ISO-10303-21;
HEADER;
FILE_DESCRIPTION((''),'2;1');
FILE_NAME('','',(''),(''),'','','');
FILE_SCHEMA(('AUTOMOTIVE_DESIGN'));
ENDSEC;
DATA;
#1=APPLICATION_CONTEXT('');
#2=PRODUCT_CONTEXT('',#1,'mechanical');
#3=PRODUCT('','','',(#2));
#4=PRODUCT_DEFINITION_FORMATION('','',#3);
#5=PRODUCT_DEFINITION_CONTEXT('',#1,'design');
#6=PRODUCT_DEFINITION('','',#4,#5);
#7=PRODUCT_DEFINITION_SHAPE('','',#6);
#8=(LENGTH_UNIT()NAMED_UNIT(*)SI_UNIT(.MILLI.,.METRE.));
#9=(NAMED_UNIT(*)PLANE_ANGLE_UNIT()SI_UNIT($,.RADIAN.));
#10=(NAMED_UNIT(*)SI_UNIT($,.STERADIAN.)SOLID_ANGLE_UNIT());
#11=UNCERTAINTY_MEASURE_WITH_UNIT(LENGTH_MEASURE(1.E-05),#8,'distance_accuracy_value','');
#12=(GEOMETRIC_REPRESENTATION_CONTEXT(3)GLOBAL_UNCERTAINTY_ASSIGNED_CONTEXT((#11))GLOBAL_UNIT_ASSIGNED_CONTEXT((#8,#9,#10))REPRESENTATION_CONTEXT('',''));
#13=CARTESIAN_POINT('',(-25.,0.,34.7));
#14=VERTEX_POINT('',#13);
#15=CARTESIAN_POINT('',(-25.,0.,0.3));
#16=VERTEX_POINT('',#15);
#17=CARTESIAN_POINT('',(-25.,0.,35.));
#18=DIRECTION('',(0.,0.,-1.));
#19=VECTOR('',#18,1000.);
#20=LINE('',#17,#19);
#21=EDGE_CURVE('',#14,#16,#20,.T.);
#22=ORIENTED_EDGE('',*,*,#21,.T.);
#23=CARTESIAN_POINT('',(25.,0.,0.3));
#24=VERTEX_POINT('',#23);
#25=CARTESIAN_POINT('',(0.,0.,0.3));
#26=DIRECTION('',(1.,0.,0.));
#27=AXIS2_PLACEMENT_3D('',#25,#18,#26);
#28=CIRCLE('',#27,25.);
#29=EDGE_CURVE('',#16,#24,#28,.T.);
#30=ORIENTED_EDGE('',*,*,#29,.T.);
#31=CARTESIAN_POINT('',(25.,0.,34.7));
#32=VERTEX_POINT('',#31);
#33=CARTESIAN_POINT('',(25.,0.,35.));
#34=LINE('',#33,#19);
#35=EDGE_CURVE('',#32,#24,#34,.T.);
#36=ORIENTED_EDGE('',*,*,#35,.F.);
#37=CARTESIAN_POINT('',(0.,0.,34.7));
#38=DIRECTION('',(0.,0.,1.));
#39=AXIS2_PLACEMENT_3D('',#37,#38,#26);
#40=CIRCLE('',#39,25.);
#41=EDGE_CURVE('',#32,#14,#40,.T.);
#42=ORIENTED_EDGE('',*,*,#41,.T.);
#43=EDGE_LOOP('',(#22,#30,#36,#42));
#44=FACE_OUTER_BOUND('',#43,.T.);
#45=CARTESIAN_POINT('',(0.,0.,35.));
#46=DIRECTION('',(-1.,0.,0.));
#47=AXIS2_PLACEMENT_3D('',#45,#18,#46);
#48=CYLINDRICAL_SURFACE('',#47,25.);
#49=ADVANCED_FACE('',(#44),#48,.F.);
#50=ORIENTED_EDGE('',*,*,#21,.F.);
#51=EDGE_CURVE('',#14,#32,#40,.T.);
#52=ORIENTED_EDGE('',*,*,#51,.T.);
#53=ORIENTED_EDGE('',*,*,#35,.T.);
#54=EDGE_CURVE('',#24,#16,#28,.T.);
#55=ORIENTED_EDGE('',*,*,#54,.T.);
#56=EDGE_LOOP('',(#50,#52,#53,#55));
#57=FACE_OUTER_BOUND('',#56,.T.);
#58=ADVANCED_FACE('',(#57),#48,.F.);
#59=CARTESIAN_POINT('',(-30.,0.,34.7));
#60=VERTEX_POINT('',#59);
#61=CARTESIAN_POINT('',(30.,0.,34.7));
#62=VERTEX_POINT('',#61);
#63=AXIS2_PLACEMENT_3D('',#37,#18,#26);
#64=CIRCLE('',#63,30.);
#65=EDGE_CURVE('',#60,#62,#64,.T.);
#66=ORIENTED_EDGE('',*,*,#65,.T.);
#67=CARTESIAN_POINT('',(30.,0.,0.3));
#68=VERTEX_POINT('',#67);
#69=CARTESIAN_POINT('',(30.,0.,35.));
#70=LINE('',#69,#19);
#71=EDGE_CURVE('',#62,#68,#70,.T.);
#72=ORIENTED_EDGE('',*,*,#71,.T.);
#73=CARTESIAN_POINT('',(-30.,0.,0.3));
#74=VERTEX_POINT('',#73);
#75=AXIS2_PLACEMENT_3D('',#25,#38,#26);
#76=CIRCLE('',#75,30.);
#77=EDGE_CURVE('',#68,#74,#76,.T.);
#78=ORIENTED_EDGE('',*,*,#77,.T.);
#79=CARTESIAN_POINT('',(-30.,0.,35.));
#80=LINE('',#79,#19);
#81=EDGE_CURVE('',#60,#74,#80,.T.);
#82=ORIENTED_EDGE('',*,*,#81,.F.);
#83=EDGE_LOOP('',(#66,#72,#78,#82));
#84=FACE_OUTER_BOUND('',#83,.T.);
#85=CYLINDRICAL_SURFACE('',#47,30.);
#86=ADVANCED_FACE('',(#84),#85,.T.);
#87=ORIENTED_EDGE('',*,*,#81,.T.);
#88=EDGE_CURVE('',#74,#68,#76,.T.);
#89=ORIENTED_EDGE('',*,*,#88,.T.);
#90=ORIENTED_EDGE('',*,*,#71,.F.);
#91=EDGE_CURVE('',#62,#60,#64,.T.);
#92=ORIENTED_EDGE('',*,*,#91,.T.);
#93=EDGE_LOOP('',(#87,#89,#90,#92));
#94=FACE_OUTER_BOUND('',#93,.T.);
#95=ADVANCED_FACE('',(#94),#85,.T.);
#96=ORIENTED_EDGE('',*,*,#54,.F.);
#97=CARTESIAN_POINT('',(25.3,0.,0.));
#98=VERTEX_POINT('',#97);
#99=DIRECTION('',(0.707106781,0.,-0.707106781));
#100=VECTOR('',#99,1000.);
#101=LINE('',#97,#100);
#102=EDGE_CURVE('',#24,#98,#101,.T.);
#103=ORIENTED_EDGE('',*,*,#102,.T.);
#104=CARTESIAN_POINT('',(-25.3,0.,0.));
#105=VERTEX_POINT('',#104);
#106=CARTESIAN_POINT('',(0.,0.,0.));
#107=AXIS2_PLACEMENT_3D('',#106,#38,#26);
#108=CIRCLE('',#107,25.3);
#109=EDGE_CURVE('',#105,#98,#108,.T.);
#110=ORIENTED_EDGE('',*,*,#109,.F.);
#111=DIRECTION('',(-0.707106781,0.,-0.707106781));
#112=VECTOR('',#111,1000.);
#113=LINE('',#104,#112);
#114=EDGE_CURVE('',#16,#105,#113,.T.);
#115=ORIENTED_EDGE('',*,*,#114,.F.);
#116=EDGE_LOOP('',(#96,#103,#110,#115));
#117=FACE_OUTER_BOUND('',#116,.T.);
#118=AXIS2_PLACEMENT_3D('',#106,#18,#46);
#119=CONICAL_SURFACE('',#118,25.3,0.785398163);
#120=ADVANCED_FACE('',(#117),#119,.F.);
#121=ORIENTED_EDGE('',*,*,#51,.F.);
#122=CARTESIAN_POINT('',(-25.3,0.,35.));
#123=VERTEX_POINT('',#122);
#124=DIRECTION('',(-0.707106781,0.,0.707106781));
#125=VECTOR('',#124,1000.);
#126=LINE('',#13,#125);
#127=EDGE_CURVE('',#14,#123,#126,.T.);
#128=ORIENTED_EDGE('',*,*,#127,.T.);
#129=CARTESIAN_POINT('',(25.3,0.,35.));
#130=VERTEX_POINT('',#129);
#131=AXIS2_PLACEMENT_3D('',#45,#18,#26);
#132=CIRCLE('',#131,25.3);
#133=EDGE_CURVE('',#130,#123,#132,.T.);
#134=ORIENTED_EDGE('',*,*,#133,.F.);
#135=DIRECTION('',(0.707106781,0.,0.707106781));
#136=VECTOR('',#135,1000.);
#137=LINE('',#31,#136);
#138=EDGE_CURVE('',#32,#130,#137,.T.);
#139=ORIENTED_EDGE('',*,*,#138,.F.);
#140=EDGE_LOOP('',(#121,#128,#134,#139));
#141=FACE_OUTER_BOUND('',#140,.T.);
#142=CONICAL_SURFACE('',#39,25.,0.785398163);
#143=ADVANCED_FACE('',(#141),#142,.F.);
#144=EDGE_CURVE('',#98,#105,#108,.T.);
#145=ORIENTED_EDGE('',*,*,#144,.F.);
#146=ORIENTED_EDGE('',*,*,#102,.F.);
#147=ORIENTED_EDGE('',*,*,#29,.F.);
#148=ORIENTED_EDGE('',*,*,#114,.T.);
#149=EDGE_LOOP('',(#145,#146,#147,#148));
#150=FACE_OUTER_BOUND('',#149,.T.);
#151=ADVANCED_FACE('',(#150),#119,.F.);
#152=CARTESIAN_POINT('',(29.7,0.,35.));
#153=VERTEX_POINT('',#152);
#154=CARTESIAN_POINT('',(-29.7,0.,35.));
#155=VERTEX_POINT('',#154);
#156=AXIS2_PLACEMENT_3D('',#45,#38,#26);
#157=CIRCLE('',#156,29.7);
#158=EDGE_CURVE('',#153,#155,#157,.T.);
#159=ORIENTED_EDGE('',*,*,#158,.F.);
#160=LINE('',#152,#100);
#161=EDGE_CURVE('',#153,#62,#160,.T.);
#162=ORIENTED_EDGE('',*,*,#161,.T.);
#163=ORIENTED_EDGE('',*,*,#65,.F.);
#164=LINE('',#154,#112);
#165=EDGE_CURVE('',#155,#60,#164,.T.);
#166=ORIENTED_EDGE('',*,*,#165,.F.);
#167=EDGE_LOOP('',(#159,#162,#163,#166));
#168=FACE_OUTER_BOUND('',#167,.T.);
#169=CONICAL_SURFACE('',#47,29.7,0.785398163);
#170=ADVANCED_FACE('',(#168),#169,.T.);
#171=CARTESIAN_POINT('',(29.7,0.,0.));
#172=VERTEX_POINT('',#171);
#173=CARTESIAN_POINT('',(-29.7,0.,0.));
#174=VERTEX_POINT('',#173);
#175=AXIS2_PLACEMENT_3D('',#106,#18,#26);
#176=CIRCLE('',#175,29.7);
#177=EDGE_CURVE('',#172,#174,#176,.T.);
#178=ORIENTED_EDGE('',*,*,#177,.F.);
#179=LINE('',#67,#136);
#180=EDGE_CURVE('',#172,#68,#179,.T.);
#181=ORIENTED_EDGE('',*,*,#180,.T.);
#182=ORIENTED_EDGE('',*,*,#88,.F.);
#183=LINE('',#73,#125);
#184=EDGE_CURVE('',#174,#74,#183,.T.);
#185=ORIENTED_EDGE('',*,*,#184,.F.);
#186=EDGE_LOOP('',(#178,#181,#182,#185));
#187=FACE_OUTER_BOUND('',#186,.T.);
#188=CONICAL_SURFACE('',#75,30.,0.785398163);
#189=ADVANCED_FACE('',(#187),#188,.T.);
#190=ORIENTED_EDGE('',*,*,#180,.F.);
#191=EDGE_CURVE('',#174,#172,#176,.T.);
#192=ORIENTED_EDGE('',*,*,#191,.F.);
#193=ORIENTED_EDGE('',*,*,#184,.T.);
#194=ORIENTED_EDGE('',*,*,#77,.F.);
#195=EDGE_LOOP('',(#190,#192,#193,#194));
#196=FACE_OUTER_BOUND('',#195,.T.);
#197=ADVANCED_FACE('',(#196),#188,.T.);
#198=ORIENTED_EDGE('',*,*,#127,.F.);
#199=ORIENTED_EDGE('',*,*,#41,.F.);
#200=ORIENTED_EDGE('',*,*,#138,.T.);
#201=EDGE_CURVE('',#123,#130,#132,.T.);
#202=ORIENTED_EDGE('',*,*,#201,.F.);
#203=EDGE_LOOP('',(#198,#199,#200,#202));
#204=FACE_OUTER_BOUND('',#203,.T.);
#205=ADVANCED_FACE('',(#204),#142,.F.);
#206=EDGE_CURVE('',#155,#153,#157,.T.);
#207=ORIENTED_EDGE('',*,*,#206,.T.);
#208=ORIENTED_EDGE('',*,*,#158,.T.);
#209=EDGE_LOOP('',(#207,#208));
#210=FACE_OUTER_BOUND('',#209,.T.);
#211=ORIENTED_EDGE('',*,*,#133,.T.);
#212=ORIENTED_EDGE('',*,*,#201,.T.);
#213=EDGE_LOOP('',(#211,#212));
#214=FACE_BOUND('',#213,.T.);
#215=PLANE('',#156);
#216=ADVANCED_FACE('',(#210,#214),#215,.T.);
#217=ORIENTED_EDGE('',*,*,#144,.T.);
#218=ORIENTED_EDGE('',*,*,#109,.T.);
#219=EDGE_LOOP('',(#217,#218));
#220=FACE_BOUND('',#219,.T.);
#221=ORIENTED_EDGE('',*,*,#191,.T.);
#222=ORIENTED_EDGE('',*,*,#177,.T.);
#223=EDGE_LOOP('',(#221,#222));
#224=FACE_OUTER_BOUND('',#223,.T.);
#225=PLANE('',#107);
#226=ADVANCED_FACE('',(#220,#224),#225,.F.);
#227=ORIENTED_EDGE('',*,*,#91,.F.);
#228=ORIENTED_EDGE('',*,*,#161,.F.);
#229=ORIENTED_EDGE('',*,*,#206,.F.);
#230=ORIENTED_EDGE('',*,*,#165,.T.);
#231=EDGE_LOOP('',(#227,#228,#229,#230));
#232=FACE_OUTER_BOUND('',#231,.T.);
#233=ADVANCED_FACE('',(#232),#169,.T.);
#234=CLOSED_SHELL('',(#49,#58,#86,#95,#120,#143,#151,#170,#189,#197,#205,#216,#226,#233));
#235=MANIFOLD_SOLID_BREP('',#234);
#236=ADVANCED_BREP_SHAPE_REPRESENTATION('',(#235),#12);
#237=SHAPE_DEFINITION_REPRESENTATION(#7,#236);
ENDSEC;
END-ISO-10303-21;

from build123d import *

# Parameters (mm, degrees)
SKETCH1_R           = 30
SKETCH1_R_2         = 25
BOSS_EXTRUDE1_DEPTH = 35
CHAMFER1_SIZE       = 0.3


with BuildPart() as part:
    # Sketch1 → Boss-Extrude1 (new body)
    with BuildSketch(Plane.XY):
        Circle(SKETCH1_R)
        Circle(SKETCH1_R_2, mode=Mode.SUBTRACT)
    extrude(amount=BOSS_EXTRUDE1_DEPTH)

    # Chamfer1
    chamfer1_edges = [part.edges().sort_by_distance(p)[0] for p in [
        (-30, 0, 0),
        (-30, 0, 35),
        (-25, 0, 0),
        (-25, 0, 35),
    ]]
    chamfer(chamfer1_edges, length=CHAMFER1_SIZE)


solid = part.part
